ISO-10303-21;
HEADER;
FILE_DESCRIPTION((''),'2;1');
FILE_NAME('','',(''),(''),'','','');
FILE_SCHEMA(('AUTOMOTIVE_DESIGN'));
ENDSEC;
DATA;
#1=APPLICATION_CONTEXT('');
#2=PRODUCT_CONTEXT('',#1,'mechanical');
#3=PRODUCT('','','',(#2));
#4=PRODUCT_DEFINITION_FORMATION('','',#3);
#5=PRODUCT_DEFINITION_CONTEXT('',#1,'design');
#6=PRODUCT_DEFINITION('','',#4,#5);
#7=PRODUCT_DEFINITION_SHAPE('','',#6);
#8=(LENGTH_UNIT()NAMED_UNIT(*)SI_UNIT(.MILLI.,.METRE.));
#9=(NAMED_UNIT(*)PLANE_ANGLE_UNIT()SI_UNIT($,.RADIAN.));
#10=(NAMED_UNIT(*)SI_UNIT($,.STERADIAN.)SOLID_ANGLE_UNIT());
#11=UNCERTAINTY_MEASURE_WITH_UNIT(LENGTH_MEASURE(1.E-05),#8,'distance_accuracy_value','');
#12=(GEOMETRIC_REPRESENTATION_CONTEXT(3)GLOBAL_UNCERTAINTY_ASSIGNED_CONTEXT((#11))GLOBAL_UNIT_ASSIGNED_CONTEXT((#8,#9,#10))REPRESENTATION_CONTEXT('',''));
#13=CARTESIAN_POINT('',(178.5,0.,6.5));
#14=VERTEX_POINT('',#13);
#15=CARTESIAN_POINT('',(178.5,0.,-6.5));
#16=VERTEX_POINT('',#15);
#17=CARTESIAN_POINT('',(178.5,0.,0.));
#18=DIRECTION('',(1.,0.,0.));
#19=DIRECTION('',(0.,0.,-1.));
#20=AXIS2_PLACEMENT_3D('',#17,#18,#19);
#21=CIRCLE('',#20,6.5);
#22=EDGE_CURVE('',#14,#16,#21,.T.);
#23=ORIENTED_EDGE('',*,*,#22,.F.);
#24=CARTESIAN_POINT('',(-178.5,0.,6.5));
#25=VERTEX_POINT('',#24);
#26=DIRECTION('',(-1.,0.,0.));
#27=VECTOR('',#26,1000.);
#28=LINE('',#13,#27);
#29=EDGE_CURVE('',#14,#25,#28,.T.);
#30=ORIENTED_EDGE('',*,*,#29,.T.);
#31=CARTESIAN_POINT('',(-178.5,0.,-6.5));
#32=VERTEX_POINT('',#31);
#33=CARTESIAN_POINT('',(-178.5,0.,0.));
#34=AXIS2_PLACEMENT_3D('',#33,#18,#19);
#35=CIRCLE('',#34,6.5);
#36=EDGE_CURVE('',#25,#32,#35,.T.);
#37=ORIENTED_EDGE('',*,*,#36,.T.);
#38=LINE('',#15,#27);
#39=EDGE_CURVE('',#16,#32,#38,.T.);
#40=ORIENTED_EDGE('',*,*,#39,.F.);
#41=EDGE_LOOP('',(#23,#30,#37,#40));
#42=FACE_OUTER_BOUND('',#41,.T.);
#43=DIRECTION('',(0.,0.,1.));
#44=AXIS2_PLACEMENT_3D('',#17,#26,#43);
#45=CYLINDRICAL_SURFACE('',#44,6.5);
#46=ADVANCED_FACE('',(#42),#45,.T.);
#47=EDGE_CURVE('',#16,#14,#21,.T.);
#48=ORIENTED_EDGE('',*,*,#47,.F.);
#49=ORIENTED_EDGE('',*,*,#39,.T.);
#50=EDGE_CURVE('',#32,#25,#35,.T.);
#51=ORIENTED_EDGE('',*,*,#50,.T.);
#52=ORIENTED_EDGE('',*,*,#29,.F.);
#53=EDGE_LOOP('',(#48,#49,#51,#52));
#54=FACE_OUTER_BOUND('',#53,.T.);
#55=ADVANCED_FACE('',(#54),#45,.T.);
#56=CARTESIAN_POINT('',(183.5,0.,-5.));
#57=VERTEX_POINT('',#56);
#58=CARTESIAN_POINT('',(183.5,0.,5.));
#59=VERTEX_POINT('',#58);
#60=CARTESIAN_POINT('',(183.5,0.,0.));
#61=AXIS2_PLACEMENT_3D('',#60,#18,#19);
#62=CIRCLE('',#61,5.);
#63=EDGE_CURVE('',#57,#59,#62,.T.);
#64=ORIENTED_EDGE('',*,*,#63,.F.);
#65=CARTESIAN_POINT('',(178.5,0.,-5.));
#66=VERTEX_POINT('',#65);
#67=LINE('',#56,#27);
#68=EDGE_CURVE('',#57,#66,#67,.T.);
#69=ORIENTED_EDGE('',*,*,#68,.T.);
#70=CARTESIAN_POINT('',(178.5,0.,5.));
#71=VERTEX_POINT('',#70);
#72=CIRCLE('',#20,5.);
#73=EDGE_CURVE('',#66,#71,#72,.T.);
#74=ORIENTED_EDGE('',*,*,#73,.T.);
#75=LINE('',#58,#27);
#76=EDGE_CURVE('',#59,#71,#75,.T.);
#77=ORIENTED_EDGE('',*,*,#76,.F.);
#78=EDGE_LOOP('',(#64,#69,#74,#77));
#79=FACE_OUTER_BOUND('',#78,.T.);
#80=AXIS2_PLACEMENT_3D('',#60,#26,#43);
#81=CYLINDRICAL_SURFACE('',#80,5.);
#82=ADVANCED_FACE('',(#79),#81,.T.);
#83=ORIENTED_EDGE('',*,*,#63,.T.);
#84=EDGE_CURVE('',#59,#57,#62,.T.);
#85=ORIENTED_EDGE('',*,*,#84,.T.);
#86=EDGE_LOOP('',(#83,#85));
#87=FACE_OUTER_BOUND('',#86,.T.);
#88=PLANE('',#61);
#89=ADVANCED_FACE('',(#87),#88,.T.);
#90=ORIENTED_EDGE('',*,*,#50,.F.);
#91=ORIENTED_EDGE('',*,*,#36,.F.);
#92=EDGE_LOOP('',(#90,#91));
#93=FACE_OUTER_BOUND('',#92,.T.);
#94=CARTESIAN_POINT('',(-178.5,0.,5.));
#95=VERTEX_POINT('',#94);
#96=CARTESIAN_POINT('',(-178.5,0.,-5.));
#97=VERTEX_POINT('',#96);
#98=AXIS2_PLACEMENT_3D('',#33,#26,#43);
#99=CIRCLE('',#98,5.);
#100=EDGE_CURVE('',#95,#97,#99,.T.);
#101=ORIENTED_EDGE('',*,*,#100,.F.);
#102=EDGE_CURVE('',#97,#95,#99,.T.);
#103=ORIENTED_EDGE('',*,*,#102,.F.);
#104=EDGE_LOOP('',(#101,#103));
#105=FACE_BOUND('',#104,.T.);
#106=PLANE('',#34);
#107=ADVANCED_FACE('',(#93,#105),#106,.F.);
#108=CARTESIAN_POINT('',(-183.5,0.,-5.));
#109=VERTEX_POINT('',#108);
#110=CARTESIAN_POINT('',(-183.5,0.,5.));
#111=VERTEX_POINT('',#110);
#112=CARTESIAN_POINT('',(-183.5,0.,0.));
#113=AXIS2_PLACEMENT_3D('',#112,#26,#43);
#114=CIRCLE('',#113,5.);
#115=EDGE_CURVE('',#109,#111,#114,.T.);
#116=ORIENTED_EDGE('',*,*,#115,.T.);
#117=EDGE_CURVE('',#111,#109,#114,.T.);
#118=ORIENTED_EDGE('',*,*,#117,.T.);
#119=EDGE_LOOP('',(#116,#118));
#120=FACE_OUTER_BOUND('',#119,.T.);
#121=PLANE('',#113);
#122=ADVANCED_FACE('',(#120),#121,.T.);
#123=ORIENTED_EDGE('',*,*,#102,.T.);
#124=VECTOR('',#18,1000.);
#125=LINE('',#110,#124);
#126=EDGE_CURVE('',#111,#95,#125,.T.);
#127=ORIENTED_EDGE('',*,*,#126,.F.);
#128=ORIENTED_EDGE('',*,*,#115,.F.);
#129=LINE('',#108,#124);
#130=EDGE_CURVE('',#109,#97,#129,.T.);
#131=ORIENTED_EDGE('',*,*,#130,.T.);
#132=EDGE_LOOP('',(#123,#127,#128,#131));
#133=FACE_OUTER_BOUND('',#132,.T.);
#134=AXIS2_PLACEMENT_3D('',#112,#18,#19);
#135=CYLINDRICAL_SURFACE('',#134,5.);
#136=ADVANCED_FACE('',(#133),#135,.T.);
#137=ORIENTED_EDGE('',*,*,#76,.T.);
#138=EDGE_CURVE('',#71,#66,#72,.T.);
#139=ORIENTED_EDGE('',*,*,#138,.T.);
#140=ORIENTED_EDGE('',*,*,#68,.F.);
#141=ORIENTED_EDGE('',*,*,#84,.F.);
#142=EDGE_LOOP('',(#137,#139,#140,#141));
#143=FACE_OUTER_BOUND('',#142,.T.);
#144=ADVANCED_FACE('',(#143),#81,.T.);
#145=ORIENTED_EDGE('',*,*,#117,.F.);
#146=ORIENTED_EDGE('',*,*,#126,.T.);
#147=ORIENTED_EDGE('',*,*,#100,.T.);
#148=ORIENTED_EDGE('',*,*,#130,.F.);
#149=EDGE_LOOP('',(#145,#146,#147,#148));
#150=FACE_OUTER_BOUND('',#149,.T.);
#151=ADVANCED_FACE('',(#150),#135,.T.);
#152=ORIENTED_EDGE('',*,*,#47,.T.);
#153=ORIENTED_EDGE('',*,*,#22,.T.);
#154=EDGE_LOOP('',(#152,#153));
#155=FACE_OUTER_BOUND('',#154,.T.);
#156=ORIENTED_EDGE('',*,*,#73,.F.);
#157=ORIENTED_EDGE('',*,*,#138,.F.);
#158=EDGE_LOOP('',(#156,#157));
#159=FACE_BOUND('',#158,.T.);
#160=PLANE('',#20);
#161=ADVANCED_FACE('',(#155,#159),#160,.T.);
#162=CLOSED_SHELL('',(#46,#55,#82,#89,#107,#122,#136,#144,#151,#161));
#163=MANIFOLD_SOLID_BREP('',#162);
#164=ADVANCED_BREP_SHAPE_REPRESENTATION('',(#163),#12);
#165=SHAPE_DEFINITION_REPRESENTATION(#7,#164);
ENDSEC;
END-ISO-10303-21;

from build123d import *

# Parameters (mm, degrees)
SKETCH1_R           = 6.5
BOSS_EXTRUDE1_DEPTH = 178.5
SKETCH2_R           = 5
BOSS_EXTRUDE2_DEPTH = 5
BOSS_EXTRUDE3_START = 5
SKETCH3_R           = 5
BOSS_EXTRUDE3_DEPTH = 5


with BuildPart() as part:
    # Sketch1 → Boss-Extrude1 (new, symmetric)
    with BuildSketch(Plane(origin=(0, 0, 0), x_dir=(0, 0, -1), z_dir=(1, 0, 0))):
        Circle(SKETCH1_R)
    extrude(amount=BOSS_EXTRUDE1_DEPTH, both=True)

    # Sketch2 → Boss-Extrude2 (add)
    with BuildSketch(Plane(origin=(178.5, 0, 0), x_dir=(0, 0, -1), z_dir=(1, 0, 0))):
        Circle(SKETCH2_R)
    extrude(amount=BOSS_EXTRUDE2_DEPTH)

    # Sketch3 → Boss-Extrude3 (add)
    with BuildSketch(Plane.ZY.offset(178.5).offset(BOSS_EXTRUDE3_START)):
        with Locations(Location((0, 0, 0), (0, 0, 180))):
            Circle(SKETCH3_R)
    extrude(amount=-BOSS_EXTRUDE3_DEPTH)


solid = part.part
